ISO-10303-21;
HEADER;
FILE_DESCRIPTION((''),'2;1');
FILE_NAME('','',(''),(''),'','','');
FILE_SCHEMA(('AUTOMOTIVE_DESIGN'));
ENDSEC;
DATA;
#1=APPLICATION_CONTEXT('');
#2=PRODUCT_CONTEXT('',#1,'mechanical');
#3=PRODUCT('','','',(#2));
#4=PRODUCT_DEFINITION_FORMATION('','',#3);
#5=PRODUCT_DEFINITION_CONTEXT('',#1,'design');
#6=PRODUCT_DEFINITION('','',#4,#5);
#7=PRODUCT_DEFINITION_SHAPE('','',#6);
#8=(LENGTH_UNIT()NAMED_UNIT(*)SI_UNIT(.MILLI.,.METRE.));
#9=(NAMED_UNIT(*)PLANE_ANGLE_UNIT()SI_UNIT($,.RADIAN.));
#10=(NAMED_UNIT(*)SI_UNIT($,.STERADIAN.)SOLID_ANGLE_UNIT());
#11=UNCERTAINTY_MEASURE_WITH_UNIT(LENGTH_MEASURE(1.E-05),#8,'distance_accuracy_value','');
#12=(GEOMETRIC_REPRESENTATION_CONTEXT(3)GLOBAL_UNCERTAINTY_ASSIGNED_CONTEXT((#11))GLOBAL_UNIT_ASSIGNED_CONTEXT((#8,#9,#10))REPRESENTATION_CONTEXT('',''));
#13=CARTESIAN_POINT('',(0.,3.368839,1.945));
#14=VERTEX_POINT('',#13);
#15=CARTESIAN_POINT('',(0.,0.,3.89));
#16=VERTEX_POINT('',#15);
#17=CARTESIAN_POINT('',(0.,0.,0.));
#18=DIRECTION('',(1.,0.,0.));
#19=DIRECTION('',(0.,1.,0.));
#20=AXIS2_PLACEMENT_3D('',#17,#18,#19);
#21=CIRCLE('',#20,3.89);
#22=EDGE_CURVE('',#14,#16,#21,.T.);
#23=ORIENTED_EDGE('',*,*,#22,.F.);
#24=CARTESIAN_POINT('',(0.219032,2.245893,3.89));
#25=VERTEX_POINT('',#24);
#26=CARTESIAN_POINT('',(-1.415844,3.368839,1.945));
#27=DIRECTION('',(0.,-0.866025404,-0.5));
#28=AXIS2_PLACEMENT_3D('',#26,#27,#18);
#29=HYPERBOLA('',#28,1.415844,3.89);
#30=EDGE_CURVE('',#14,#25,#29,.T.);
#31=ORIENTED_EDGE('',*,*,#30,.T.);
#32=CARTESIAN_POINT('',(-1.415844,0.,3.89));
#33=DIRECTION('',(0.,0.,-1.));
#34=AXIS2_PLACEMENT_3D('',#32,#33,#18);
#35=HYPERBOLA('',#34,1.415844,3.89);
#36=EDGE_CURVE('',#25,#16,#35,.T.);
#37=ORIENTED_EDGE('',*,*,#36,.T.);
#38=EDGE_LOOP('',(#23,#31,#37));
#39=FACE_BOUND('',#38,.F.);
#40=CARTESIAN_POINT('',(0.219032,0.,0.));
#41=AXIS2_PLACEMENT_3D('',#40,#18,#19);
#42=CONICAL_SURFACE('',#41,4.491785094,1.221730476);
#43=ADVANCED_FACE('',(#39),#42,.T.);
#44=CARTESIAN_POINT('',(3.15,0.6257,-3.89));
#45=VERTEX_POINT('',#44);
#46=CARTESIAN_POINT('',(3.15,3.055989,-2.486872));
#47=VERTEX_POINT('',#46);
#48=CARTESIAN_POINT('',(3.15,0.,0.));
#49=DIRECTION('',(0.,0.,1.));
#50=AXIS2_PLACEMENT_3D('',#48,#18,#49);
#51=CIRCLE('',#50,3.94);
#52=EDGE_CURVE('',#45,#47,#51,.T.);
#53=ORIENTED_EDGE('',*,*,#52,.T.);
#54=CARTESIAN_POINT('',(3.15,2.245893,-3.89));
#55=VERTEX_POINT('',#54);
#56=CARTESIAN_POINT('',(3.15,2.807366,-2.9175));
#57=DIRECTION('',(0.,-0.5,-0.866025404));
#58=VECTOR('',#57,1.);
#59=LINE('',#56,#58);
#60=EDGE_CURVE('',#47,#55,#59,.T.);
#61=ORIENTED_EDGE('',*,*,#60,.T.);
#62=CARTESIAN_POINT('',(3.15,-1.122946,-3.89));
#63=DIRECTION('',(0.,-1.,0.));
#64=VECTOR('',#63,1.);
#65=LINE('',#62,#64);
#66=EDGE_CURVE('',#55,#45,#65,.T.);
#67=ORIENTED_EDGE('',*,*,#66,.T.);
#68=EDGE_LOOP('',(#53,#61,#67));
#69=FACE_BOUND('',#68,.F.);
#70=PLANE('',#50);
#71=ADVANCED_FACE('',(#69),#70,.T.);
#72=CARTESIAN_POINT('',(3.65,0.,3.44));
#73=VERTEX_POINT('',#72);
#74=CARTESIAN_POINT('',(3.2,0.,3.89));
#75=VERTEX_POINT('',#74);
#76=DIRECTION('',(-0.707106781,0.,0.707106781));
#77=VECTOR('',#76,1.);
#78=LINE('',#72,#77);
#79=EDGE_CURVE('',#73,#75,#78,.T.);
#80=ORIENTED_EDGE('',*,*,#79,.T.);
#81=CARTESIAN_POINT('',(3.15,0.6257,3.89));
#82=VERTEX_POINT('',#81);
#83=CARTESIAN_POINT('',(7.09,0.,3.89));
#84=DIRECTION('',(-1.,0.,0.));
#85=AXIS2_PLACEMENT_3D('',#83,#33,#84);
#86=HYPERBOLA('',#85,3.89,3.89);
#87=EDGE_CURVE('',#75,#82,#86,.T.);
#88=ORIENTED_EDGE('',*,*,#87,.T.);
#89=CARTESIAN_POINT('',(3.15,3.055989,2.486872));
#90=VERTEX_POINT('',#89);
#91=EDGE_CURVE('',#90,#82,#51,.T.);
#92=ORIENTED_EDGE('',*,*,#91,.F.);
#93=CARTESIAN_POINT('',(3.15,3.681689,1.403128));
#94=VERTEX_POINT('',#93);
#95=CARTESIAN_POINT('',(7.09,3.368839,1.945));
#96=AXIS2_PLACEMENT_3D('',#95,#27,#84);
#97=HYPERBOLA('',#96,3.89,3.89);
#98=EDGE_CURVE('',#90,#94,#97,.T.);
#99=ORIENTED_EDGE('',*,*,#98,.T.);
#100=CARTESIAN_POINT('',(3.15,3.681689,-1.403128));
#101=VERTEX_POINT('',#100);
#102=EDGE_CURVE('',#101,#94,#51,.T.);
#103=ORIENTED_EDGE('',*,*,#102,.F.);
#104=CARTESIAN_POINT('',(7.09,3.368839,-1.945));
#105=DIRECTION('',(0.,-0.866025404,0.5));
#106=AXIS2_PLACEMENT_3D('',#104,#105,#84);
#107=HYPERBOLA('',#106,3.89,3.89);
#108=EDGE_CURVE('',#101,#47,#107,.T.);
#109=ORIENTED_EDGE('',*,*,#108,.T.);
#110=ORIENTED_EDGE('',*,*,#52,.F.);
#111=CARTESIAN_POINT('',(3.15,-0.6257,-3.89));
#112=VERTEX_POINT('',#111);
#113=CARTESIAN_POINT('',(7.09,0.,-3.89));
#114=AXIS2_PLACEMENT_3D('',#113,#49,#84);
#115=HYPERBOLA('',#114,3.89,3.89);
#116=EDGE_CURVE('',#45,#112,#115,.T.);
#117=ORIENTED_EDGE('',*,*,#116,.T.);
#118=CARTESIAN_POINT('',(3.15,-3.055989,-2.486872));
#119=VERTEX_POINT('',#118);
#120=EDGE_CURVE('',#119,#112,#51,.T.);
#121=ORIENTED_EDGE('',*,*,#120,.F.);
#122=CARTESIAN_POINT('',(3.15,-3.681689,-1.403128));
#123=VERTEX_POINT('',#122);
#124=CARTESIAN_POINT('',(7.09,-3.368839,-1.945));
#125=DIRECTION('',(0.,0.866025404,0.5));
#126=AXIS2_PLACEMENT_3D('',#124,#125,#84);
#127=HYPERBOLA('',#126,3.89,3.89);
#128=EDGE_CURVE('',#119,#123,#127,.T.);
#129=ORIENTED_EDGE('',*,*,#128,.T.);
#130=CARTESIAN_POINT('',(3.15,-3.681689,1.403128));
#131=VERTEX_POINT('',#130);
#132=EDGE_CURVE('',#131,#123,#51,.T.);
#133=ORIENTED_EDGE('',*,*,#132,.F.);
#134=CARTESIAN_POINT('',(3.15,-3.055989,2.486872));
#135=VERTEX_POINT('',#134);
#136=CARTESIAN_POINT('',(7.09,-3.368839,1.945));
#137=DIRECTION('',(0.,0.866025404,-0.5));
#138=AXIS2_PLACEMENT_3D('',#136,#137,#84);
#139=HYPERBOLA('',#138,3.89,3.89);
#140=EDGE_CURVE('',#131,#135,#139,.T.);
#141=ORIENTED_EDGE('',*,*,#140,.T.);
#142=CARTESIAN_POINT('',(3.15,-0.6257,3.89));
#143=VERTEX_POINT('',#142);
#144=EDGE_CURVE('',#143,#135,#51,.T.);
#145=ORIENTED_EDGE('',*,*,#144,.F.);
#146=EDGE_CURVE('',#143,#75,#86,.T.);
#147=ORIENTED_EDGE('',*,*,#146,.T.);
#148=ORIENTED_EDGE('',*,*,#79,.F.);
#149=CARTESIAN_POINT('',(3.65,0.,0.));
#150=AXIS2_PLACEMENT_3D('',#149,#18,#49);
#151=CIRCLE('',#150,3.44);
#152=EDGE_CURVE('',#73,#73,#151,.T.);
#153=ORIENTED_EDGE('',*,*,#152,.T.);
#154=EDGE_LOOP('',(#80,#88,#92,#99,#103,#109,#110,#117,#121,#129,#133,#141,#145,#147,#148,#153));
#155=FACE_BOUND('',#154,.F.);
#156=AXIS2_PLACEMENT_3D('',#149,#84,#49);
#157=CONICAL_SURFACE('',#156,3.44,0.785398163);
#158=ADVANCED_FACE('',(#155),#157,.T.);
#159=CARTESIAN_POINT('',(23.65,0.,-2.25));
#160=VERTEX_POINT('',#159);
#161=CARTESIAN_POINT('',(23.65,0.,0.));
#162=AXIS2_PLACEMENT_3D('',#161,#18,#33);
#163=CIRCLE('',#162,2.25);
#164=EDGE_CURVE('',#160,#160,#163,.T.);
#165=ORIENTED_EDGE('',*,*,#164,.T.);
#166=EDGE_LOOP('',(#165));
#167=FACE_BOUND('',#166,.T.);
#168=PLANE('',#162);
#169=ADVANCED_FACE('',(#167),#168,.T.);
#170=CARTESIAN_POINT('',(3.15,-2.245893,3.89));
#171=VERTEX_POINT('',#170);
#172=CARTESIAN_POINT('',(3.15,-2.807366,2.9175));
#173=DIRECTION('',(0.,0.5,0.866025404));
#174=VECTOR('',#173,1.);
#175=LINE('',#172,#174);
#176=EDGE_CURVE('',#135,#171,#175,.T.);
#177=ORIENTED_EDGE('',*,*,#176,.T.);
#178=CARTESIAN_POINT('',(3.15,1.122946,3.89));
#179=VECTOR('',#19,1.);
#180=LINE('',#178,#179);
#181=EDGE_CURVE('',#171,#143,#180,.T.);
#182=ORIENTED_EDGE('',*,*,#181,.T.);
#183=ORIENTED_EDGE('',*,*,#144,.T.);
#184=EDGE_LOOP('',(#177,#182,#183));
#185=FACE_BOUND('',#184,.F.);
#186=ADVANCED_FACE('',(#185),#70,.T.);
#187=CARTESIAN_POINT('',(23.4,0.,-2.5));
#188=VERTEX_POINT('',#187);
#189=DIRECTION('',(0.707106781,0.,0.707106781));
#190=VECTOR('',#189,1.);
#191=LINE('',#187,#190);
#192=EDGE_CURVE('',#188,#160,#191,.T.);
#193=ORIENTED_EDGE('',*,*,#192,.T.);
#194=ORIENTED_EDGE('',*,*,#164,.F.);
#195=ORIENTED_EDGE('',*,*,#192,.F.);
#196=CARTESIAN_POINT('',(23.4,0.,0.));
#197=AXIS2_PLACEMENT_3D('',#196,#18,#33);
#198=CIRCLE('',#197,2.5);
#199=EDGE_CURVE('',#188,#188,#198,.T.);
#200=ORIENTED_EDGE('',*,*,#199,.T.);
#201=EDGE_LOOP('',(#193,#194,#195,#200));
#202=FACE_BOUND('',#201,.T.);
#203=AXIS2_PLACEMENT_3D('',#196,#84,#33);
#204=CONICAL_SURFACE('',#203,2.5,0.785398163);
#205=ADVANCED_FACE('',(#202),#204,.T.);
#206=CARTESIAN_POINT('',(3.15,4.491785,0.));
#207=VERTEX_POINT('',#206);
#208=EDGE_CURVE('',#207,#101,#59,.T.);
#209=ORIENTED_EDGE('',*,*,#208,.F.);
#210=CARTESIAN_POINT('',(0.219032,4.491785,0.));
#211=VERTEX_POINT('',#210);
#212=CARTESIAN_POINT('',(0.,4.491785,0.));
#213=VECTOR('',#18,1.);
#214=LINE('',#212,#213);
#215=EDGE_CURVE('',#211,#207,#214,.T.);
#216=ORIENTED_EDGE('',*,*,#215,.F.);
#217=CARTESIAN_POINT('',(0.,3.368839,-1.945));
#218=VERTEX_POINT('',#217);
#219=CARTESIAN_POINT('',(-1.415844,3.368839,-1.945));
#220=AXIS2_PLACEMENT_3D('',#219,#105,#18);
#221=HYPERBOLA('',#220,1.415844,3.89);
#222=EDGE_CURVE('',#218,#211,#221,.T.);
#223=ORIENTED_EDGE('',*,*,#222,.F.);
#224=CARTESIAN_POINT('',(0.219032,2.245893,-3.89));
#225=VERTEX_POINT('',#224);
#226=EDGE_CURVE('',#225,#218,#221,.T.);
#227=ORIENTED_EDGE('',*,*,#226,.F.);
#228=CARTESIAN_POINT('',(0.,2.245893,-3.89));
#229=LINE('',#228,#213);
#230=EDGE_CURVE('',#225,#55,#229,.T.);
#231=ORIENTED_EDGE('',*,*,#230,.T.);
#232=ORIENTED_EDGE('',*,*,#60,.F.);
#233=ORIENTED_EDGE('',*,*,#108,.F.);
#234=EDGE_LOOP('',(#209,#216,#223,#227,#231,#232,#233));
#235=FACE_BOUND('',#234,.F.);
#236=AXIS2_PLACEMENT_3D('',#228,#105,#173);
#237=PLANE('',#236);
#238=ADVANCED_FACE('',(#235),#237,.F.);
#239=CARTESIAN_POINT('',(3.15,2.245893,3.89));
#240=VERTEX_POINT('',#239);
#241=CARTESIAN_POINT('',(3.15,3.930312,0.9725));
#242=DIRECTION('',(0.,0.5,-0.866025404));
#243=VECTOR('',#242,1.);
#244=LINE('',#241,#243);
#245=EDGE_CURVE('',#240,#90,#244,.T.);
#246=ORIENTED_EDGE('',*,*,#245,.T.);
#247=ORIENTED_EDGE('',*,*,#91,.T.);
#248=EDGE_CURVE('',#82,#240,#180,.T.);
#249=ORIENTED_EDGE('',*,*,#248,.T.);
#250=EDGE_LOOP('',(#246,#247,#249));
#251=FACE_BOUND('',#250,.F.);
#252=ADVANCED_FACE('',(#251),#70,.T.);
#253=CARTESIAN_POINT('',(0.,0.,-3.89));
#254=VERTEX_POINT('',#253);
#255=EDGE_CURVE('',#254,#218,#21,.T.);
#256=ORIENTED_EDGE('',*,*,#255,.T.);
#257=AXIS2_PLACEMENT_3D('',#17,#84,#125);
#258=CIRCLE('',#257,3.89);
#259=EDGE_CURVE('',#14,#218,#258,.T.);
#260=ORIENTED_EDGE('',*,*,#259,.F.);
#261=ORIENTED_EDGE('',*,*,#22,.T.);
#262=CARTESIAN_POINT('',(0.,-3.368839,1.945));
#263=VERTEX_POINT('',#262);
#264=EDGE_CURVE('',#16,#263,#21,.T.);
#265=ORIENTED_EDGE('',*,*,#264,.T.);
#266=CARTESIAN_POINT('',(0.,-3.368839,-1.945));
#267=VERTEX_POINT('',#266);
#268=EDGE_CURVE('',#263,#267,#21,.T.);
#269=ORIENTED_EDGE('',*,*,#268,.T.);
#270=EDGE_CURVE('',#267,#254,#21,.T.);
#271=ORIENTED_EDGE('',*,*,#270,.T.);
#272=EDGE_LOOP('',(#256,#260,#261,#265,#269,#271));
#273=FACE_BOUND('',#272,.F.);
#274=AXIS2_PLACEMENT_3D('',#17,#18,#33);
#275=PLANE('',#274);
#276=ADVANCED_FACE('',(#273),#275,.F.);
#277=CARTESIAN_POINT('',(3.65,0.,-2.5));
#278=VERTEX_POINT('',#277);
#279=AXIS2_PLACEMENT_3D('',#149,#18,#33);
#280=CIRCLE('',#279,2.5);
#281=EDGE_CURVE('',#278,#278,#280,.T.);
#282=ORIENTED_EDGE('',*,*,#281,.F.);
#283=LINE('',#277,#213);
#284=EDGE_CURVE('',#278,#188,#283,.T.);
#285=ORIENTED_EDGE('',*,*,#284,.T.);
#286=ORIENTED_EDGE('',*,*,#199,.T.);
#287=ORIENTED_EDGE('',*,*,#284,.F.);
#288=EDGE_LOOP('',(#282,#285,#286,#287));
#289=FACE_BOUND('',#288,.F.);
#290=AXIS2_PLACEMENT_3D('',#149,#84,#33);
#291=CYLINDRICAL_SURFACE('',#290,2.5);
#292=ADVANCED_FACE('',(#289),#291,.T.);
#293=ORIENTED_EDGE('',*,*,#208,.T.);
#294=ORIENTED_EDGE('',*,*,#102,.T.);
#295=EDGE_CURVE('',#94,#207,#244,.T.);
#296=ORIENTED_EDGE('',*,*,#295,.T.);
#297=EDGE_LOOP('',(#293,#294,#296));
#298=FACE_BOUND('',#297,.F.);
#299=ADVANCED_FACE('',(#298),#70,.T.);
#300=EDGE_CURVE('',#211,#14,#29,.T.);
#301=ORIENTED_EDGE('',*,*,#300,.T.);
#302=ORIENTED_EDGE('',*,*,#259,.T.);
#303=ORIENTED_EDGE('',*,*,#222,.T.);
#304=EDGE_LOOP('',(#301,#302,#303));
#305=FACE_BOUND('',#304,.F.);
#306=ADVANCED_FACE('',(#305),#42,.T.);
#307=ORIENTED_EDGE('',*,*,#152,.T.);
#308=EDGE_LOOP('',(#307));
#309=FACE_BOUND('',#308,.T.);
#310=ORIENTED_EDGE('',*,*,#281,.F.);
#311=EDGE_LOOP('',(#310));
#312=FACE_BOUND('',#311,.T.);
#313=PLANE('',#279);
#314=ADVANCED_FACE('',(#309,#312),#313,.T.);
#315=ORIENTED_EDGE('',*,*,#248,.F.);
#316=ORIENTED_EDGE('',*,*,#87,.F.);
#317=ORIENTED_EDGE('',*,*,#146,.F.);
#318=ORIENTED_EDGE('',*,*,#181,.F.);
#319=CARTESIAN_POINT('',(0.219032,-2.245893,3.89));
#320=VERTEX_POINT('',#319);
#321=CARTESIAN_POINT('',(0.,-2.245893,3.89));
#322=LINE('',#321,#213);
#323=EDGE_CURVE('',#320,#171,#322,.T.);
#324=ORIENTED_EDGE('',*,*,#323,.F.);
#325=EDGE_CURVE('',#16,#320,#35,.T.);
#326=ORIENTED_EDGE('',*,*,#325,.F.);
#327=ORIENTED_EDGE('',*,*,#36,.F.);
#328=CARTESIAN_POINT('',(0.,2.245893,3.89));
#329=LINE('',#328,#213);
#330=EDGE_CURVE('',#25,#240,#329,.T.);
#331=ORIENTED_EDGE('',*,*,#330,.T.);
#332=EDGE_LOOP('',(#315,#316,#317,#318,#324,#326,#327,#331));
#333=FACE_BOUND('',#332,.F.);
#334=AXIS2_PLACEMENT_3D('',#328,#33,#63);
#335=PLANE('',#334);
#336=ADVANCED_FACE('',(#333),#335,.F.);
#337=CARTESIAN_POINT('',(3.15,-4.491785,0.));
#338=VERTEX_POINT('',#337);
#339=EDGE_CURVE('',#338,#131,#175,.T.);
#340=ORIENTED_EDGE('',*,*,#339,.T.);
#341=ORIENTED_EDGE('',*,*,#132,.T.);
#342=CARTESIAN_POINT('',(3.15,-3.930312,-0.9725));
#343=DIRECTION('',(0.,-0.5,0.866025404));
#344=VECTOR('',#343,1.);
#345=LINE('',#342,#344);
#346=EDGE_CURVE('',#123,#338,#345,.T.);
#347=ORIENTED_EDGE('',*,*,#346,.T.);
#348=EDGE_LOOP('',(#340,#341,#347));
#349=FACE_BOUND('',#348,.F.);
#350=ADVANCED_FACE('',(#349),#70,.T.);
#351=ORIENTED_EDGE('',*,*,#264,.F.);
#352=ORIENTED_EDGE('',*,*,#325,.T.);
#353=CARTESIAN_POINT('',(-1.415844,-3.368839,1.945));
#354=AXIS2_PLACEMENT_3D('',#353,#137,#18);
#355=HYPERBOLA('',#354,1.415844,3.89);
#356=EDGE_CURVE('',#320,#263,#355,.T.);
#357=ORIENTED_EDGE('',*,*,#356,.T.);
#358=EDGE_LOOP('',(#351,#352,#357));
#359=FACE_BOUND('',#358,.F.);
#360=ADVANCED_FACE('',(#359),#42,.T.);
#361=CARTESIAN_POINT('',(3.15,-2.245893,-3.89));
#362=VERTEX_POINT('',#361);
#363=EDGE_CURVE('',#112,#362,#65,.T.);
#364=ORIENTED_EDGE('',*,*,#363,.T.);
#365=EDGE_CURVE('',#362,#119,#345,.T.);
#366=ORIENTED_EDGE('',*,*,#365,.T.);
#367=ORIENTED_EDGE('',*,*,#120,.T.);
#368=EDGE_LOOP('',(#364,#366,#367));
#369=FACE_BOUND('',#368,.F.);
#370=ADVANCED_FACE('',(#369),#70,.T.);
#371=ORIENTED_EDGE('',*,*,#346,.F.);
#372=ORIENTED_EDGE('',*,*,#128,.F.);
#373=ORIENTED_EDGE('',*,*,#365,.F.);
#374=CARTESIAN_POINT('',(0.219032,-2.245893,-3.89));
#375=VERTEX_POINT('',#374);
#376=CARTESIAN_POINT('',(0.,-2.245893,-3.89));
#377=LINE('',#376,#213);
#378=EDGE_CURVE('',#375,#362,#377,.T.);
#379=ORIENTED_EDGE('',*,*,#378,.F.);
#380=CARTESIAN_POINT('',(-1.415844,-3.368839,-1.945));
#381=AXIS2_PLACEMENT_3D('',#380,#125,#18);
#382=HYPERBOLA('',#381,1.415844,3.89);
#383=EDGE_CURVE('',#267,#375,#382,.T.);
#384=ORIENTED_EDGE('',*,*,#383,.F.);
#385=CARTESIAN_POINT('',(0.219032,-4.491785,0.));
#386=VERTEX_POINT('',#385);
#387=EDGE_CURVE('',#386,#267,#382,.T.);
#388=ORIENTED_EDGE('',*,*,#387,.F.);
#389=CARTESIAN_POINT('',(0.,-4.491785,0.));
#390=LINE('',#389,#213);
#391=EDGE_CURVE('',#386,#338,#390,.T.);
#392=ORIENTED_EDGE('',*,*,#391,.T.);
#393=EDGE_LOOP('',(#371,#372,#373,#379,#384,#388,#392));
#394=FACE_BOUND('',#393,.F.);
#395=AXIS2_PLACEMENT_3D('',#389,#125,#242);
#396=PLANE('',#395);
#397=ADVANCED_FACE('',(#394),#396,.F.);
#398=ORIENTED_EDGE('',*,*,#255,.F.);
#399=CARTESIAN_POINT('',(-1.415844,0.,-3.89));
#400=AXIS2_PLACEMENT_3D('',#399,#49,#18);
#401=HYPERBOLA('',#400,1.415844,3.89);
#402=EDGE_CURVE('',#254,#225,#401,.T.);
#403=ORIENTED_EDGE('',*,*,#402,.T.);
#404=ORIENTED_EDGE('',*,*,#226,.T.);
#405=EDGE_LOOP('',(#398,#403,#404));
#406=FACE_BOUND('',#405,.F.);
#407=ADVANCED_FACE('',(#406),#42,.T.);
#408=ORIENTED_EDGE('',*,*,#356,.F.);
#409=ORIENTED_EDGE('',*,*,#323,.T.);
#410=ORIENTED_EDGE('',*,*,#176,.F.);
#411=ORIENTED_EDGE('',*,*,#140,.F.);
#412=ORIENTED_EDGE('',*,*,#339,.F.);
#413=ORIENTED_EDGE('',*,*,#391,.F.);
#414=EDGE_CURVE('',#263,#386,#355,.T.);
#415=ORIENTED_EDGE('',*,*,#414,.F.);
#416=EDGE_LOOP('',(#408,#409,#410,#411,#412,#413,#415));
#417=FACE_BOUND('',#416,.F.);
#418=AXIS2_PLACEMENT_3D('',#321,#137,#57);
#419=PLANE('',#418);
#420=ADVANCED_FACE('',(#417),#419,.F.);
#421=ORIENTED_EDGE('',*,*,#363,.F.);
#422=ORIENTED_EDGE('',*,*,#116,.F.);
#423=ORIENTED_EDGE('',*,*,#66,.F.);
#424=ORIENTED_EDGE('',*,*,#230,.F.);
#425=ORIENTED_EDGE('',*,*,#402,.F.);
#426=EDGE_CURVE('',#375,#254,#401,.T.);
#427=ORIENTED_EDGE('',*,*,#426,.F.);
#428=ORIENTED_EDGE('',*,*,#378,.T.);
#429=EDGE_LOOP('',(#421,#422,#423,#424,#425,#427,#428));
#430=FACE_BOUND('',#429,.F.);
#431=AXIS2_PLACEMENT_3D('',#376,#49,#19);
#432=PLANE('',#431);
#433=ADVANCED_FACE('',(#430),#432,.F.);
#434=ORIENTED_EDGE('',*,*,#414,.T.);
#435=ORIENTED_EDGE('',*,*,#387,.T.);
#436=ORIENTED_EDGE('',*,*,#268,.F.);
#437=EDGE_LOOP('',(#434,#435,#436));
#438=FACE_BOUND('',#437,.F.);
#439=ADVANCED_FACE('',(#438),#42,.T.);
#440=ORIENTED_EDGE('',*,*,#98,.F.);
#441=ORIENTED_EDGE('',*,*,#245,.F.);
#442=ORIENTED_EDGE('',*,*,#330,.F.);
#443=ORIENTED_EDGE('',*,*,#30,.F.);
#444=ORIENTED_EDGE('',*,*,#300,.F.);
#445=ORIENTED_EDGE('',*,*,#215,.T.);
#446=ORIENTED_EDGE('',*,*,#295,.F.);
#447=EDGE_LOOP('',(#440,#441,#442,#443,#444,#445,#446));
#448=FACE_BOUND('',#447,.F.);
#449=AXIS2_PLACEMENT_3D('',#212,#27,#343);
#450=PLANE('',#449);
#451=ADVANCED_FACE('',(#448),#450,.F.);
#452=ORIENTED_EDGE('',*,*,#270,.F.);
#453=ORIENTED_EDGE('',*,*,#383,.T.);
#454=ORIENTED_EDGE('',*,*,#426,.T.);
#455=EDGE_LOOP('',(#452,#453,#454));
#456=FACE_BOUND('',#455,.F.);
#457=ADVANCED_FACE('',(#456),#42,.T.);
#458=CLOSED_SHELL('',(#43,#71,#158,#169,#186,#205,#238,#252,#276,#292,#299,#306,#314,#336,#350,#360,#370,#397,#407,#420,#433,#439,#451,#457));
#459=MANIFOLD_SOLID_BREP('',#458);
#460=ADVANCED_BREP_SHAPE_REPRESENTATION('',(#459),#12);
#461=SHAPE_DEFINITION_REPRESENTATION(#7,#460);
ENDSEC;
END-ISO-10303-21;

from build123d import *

# Parameters (mm, degrees)
BASEHEAD_DEPTH = 3.65
SKETCH5_R      = 2.5
BASEBODY_DEPTH = 20
CHAMFER1_SIZE  = 0.25


with BuildPart() as part:
    # Sketch2 → BaseHead (new body)
    with BuildSketch(Plane(origin=(0, 0, 0), x_dir=(0, 0, -1), z_dir=(1, 0, 0))):
        Polygon((3.89, -2.245892547), (3.89, 2.245892547), (0, 4.491785094), (-3.89, 2.245892547), (-3.89, -2.245892547), (0, -4.491785094), align=None)
    extrude(amount=BASEHEAD_DEPTH)

    # Sketch3 → BearingFace (revolve, cut)
    with BuildSketch(Plane.XY, mode=Mode.PRIVATE) as bearingface_sk:
        Polygon((3.65, 4.491785094), (3.65, 3.44), (3.15, 3.94), (3.15, 4.491785094), align=None)
    revolve(bearingface_sk.sketch.rotate(Axis((-0.957090588, 0, 0), (1, 0, 0)), 90), axis=Axis((-0.957090588, 0, 0), (1, 0, 0)), mode=Mode.SUBTRACT)

    # Sketch4 → HeadChamfer (revolve, cut)
    with BuildSketch(Plane.XY):
        Polygon((0, 4.491785094), (0.219031862, 4.491785094), (0, 3.89), align=None)
    revolve(axis=Axis((-0.493528746, 0, 0), (1, 0, 0)), mode=Mode.SUBTRACT)

    # Sketch5 → BaseBody (add)
    with BuildSketch(Plane(origin=(3.65, 0, 0), x_dir=(0, 0, -1), z_dir=(1, 0, 0))):
        Circle(SKETCH5_R)
    extrude(amount=BASEBODY_DEPTH)

    # Chamfer1
    chamfer1_edges = [part.edges().sort_by_distance(p)[0] for p in [
        (23.65, 0, 2.5),
    ]]
    chamfer(chamfer1_edges, length=CHAMFER1_SIZE)


solid = part.part
